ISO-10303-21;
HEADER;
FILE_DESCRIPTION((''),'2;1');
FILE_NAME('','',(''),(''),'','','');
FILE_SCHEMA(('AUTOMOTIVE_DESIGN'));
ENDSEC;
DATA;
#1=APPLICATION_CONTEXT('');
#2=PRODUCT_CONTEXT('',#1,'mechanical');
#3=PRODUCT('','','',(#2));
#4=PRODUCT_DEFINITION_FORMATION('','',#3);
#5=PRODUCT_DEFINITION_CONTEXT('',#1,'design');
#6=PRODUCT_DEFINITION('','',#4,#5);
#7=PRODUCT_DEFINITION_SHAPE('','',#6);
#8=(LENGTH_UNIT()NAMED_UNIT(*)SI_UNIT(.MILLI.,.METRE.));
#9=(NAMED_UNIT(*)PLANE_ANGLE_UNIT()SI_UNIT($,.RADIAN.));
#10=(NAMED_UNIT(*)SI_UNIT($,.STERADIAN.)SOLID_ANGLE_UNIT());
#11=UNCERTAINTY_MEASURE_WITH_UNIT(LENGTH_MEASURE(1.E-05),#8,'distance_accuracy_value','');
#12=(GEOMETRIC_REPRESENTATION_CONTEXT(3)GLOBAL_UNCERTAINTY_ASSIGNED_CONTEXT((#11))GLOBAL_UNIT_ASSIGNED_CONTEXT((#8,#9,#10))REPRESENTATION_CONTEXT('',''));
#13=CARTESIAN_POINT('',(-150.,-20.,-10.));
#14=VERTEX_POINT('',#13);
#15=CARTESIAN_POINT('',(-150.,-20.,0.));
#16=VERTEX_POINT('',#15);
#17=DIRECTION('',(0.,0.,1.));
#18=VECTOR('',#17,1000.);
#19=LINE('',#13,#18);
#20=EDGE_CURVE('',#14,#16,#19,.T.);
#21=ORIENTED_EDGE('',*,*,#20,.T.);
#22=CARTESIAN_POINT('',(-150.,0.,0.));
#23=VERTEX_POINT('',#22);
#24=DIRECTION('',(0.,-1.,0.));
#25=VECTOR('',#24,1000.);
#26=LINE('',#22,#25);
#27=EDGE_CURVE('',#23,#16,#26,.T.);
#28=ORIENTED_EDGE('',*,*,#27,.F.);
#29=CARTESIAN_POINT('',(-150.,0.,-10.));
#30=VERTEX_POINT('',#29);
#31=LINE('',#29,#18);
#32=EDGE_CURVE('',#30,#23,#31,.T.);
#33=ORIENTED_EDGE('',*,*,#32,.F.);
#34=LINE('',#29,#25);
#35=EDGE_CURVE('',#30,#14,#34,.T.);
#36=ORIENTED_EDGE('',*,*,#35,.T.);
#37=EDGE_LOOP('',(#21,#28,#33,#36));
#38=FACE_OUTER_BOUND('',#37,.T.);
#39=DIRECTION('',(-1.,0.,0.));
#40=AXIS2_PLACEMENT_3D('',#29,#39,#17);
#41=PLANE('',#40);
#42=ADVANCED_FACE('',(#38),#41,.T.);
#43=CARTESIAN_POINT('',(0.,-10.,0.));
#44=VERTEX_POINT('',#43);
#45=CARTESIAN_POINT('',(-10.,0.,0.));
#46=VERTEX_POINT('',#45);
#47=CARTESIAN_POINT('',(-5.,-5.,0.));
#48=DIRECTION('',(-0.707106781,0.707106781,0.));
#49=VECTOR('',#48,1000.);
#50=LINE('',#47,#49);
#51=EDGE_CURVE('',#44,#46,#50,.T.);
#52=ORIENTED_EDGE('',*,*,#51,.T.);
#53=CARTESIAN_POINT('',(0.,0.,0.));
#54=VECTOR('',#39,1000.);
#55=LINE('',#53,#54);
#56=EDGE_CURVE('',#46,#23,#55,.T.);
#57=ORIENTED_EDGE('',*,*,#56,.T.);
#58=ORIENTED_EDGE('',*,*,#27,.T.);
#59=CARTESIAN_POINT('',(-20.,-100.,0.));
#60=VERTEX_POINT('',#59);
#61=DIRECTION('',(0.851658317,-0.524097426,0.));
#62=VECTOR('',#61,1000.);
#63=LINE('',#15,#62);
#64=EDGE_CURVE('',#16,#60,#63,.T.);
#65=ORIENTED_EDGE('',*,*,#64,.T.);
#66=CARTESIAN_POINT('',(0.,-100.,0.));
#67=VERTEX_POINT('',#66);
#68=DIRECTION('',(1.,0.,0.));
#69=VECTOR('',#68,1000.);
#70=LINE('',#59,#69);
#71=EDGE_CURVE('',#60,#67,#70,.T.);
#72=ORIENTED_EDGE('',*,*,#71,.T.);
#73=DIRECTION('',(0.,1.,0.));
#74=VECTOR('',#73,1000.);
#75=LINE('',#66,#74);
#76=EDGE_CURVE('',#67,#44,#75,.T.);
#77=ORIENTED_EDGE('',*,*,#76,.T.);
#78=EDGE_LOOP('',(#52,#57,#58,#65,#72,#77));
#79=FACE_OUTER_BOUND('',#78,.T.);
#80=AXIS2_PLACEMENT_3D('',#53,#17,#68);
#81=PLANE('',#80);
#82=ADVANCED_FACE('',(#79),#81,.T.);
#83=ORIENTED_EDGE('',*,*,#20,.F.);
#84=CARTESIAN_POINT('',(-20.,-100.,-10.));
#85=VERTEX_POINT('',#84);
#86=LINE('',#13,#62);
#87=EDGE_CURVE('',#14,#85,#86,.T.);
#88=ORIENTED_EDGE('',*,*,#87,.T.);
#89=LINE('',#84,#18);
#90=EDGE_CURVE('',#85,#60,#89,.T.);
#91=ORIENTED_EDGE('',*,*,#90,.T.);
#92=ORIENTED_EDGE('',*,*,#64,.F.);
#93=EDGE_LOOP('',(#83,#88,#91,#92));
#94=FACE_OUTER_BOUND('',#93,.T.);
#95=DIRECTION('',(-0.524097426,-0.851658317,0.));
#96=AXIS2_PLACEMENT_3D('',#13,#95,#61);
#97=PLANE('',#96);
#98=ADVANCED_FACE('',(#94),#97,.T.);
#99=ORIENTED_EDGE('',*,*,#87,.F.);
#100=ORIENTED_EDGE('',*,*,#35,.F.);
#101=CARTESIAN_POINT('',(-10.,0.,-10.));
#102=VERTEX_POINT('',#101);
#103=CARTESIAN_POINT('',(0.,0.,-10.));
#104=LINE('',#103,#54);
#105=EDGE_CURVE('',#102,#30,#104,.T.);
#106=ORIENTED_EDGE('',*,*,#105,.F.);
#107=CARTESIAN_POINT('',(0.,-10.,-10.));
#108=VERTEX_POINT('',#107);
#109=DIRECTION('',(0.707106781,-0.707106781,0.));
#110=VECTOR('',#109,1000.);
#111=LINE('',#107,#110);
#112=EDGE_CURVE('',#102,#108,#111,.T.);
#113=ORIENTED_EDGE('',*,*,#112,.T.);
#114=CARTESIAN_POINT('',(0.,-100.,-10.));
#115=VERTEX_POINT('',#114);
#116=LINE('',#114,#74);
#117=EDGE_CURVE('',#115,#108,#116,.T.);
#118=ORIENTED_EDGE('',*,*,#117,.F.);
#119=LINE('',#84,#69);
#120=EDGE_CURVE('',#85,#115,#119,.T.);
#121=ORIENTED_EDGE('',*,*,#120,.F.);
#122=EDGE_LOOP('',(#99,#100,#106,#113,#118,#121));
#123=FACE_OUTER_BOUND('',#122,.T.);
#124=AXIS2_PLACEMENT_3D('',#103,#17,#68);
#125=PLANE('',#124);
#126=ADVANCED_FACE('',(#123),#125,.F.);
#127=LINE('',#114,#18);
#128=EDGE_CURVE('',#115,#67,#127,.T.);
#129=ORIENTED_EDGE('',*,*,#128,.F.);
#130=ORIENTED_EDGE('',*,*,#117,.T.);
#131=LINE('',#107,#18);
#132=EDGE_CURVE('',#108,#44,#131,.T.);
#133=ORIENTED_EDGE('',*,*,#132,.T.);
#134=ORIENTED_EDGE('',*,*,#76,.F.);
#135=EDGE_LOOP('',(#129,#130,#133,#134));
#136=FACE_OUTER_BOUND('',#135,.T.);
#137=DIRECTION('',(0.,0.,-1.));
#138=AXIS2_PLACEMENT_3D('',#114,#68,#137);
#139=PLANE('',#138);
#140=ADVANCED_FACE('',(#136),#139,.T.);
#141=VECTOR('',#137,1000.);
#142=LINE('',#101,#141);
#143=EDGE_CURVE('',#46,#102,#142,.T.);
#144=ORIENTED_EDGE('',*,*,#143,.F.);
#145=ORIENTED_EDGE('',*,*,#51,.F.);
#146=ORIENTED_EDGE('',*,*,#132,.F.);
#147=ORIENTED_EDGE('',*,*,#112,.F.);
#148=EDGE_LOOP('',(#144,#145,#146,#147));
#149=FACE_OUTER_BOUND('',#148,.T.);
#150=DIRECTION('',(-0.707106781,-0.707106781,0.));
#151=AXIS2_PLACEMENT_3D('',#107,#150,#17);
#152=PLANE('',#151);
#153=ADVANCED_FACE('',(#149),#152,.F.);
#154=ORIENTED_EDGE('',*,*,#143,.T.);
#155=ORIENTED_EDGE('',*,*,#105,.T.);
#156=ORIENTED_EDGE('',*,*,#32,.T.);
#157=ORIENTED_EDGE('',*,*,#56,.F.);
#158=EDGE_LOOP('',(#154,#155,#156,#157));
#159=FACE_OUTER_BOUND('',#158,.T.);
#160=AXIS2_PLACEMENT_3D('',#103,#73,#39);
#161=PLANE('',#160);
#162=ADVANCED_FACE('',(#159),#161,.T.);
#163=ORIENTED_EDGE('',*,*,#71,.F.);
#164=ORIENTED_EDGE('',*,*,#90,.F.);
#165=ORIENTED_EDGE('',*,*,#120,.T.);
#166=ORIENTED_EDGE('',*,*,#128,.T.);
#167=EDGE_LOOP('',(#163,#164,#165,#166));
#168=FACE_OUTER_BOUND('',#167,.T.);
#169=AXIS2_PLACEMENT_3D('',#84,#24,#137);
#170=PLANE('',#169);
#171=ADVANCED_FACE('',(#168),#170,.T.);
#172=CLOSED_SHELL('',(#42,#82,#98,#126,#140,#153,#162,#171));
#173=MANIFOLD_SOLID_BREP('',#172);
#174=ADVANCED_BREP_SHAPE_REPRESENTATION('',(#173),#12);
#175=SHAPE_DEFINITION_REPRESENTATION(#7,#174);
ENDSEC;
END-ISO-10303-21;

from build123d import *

# Parameters (mm, degrees)
BOSS_EXTRUDE1_DEPTH = 10
CHAMFER1_SIZE       = 10


with BuildPart() as part:
    # Sketch1 → Boss-Extrude1 (new body)
    with BuildSketch(Plane.XY):
        Polygon((0, 0), (-150, 0), (-150, -20), (-20, -100), (0, -100), align=None)
    extrude(amount=-BOSS_EXTRUDE1_DEPTH)

    # Chamfer1
    chamfer1_edges = [part.edges().sort_by_distance(p)[0] for p in [
        (0, 0, -5),
    ]]
    chamfer(chamfer1_edges, length=CHAMFER1_SIZE)


solid = part.part
